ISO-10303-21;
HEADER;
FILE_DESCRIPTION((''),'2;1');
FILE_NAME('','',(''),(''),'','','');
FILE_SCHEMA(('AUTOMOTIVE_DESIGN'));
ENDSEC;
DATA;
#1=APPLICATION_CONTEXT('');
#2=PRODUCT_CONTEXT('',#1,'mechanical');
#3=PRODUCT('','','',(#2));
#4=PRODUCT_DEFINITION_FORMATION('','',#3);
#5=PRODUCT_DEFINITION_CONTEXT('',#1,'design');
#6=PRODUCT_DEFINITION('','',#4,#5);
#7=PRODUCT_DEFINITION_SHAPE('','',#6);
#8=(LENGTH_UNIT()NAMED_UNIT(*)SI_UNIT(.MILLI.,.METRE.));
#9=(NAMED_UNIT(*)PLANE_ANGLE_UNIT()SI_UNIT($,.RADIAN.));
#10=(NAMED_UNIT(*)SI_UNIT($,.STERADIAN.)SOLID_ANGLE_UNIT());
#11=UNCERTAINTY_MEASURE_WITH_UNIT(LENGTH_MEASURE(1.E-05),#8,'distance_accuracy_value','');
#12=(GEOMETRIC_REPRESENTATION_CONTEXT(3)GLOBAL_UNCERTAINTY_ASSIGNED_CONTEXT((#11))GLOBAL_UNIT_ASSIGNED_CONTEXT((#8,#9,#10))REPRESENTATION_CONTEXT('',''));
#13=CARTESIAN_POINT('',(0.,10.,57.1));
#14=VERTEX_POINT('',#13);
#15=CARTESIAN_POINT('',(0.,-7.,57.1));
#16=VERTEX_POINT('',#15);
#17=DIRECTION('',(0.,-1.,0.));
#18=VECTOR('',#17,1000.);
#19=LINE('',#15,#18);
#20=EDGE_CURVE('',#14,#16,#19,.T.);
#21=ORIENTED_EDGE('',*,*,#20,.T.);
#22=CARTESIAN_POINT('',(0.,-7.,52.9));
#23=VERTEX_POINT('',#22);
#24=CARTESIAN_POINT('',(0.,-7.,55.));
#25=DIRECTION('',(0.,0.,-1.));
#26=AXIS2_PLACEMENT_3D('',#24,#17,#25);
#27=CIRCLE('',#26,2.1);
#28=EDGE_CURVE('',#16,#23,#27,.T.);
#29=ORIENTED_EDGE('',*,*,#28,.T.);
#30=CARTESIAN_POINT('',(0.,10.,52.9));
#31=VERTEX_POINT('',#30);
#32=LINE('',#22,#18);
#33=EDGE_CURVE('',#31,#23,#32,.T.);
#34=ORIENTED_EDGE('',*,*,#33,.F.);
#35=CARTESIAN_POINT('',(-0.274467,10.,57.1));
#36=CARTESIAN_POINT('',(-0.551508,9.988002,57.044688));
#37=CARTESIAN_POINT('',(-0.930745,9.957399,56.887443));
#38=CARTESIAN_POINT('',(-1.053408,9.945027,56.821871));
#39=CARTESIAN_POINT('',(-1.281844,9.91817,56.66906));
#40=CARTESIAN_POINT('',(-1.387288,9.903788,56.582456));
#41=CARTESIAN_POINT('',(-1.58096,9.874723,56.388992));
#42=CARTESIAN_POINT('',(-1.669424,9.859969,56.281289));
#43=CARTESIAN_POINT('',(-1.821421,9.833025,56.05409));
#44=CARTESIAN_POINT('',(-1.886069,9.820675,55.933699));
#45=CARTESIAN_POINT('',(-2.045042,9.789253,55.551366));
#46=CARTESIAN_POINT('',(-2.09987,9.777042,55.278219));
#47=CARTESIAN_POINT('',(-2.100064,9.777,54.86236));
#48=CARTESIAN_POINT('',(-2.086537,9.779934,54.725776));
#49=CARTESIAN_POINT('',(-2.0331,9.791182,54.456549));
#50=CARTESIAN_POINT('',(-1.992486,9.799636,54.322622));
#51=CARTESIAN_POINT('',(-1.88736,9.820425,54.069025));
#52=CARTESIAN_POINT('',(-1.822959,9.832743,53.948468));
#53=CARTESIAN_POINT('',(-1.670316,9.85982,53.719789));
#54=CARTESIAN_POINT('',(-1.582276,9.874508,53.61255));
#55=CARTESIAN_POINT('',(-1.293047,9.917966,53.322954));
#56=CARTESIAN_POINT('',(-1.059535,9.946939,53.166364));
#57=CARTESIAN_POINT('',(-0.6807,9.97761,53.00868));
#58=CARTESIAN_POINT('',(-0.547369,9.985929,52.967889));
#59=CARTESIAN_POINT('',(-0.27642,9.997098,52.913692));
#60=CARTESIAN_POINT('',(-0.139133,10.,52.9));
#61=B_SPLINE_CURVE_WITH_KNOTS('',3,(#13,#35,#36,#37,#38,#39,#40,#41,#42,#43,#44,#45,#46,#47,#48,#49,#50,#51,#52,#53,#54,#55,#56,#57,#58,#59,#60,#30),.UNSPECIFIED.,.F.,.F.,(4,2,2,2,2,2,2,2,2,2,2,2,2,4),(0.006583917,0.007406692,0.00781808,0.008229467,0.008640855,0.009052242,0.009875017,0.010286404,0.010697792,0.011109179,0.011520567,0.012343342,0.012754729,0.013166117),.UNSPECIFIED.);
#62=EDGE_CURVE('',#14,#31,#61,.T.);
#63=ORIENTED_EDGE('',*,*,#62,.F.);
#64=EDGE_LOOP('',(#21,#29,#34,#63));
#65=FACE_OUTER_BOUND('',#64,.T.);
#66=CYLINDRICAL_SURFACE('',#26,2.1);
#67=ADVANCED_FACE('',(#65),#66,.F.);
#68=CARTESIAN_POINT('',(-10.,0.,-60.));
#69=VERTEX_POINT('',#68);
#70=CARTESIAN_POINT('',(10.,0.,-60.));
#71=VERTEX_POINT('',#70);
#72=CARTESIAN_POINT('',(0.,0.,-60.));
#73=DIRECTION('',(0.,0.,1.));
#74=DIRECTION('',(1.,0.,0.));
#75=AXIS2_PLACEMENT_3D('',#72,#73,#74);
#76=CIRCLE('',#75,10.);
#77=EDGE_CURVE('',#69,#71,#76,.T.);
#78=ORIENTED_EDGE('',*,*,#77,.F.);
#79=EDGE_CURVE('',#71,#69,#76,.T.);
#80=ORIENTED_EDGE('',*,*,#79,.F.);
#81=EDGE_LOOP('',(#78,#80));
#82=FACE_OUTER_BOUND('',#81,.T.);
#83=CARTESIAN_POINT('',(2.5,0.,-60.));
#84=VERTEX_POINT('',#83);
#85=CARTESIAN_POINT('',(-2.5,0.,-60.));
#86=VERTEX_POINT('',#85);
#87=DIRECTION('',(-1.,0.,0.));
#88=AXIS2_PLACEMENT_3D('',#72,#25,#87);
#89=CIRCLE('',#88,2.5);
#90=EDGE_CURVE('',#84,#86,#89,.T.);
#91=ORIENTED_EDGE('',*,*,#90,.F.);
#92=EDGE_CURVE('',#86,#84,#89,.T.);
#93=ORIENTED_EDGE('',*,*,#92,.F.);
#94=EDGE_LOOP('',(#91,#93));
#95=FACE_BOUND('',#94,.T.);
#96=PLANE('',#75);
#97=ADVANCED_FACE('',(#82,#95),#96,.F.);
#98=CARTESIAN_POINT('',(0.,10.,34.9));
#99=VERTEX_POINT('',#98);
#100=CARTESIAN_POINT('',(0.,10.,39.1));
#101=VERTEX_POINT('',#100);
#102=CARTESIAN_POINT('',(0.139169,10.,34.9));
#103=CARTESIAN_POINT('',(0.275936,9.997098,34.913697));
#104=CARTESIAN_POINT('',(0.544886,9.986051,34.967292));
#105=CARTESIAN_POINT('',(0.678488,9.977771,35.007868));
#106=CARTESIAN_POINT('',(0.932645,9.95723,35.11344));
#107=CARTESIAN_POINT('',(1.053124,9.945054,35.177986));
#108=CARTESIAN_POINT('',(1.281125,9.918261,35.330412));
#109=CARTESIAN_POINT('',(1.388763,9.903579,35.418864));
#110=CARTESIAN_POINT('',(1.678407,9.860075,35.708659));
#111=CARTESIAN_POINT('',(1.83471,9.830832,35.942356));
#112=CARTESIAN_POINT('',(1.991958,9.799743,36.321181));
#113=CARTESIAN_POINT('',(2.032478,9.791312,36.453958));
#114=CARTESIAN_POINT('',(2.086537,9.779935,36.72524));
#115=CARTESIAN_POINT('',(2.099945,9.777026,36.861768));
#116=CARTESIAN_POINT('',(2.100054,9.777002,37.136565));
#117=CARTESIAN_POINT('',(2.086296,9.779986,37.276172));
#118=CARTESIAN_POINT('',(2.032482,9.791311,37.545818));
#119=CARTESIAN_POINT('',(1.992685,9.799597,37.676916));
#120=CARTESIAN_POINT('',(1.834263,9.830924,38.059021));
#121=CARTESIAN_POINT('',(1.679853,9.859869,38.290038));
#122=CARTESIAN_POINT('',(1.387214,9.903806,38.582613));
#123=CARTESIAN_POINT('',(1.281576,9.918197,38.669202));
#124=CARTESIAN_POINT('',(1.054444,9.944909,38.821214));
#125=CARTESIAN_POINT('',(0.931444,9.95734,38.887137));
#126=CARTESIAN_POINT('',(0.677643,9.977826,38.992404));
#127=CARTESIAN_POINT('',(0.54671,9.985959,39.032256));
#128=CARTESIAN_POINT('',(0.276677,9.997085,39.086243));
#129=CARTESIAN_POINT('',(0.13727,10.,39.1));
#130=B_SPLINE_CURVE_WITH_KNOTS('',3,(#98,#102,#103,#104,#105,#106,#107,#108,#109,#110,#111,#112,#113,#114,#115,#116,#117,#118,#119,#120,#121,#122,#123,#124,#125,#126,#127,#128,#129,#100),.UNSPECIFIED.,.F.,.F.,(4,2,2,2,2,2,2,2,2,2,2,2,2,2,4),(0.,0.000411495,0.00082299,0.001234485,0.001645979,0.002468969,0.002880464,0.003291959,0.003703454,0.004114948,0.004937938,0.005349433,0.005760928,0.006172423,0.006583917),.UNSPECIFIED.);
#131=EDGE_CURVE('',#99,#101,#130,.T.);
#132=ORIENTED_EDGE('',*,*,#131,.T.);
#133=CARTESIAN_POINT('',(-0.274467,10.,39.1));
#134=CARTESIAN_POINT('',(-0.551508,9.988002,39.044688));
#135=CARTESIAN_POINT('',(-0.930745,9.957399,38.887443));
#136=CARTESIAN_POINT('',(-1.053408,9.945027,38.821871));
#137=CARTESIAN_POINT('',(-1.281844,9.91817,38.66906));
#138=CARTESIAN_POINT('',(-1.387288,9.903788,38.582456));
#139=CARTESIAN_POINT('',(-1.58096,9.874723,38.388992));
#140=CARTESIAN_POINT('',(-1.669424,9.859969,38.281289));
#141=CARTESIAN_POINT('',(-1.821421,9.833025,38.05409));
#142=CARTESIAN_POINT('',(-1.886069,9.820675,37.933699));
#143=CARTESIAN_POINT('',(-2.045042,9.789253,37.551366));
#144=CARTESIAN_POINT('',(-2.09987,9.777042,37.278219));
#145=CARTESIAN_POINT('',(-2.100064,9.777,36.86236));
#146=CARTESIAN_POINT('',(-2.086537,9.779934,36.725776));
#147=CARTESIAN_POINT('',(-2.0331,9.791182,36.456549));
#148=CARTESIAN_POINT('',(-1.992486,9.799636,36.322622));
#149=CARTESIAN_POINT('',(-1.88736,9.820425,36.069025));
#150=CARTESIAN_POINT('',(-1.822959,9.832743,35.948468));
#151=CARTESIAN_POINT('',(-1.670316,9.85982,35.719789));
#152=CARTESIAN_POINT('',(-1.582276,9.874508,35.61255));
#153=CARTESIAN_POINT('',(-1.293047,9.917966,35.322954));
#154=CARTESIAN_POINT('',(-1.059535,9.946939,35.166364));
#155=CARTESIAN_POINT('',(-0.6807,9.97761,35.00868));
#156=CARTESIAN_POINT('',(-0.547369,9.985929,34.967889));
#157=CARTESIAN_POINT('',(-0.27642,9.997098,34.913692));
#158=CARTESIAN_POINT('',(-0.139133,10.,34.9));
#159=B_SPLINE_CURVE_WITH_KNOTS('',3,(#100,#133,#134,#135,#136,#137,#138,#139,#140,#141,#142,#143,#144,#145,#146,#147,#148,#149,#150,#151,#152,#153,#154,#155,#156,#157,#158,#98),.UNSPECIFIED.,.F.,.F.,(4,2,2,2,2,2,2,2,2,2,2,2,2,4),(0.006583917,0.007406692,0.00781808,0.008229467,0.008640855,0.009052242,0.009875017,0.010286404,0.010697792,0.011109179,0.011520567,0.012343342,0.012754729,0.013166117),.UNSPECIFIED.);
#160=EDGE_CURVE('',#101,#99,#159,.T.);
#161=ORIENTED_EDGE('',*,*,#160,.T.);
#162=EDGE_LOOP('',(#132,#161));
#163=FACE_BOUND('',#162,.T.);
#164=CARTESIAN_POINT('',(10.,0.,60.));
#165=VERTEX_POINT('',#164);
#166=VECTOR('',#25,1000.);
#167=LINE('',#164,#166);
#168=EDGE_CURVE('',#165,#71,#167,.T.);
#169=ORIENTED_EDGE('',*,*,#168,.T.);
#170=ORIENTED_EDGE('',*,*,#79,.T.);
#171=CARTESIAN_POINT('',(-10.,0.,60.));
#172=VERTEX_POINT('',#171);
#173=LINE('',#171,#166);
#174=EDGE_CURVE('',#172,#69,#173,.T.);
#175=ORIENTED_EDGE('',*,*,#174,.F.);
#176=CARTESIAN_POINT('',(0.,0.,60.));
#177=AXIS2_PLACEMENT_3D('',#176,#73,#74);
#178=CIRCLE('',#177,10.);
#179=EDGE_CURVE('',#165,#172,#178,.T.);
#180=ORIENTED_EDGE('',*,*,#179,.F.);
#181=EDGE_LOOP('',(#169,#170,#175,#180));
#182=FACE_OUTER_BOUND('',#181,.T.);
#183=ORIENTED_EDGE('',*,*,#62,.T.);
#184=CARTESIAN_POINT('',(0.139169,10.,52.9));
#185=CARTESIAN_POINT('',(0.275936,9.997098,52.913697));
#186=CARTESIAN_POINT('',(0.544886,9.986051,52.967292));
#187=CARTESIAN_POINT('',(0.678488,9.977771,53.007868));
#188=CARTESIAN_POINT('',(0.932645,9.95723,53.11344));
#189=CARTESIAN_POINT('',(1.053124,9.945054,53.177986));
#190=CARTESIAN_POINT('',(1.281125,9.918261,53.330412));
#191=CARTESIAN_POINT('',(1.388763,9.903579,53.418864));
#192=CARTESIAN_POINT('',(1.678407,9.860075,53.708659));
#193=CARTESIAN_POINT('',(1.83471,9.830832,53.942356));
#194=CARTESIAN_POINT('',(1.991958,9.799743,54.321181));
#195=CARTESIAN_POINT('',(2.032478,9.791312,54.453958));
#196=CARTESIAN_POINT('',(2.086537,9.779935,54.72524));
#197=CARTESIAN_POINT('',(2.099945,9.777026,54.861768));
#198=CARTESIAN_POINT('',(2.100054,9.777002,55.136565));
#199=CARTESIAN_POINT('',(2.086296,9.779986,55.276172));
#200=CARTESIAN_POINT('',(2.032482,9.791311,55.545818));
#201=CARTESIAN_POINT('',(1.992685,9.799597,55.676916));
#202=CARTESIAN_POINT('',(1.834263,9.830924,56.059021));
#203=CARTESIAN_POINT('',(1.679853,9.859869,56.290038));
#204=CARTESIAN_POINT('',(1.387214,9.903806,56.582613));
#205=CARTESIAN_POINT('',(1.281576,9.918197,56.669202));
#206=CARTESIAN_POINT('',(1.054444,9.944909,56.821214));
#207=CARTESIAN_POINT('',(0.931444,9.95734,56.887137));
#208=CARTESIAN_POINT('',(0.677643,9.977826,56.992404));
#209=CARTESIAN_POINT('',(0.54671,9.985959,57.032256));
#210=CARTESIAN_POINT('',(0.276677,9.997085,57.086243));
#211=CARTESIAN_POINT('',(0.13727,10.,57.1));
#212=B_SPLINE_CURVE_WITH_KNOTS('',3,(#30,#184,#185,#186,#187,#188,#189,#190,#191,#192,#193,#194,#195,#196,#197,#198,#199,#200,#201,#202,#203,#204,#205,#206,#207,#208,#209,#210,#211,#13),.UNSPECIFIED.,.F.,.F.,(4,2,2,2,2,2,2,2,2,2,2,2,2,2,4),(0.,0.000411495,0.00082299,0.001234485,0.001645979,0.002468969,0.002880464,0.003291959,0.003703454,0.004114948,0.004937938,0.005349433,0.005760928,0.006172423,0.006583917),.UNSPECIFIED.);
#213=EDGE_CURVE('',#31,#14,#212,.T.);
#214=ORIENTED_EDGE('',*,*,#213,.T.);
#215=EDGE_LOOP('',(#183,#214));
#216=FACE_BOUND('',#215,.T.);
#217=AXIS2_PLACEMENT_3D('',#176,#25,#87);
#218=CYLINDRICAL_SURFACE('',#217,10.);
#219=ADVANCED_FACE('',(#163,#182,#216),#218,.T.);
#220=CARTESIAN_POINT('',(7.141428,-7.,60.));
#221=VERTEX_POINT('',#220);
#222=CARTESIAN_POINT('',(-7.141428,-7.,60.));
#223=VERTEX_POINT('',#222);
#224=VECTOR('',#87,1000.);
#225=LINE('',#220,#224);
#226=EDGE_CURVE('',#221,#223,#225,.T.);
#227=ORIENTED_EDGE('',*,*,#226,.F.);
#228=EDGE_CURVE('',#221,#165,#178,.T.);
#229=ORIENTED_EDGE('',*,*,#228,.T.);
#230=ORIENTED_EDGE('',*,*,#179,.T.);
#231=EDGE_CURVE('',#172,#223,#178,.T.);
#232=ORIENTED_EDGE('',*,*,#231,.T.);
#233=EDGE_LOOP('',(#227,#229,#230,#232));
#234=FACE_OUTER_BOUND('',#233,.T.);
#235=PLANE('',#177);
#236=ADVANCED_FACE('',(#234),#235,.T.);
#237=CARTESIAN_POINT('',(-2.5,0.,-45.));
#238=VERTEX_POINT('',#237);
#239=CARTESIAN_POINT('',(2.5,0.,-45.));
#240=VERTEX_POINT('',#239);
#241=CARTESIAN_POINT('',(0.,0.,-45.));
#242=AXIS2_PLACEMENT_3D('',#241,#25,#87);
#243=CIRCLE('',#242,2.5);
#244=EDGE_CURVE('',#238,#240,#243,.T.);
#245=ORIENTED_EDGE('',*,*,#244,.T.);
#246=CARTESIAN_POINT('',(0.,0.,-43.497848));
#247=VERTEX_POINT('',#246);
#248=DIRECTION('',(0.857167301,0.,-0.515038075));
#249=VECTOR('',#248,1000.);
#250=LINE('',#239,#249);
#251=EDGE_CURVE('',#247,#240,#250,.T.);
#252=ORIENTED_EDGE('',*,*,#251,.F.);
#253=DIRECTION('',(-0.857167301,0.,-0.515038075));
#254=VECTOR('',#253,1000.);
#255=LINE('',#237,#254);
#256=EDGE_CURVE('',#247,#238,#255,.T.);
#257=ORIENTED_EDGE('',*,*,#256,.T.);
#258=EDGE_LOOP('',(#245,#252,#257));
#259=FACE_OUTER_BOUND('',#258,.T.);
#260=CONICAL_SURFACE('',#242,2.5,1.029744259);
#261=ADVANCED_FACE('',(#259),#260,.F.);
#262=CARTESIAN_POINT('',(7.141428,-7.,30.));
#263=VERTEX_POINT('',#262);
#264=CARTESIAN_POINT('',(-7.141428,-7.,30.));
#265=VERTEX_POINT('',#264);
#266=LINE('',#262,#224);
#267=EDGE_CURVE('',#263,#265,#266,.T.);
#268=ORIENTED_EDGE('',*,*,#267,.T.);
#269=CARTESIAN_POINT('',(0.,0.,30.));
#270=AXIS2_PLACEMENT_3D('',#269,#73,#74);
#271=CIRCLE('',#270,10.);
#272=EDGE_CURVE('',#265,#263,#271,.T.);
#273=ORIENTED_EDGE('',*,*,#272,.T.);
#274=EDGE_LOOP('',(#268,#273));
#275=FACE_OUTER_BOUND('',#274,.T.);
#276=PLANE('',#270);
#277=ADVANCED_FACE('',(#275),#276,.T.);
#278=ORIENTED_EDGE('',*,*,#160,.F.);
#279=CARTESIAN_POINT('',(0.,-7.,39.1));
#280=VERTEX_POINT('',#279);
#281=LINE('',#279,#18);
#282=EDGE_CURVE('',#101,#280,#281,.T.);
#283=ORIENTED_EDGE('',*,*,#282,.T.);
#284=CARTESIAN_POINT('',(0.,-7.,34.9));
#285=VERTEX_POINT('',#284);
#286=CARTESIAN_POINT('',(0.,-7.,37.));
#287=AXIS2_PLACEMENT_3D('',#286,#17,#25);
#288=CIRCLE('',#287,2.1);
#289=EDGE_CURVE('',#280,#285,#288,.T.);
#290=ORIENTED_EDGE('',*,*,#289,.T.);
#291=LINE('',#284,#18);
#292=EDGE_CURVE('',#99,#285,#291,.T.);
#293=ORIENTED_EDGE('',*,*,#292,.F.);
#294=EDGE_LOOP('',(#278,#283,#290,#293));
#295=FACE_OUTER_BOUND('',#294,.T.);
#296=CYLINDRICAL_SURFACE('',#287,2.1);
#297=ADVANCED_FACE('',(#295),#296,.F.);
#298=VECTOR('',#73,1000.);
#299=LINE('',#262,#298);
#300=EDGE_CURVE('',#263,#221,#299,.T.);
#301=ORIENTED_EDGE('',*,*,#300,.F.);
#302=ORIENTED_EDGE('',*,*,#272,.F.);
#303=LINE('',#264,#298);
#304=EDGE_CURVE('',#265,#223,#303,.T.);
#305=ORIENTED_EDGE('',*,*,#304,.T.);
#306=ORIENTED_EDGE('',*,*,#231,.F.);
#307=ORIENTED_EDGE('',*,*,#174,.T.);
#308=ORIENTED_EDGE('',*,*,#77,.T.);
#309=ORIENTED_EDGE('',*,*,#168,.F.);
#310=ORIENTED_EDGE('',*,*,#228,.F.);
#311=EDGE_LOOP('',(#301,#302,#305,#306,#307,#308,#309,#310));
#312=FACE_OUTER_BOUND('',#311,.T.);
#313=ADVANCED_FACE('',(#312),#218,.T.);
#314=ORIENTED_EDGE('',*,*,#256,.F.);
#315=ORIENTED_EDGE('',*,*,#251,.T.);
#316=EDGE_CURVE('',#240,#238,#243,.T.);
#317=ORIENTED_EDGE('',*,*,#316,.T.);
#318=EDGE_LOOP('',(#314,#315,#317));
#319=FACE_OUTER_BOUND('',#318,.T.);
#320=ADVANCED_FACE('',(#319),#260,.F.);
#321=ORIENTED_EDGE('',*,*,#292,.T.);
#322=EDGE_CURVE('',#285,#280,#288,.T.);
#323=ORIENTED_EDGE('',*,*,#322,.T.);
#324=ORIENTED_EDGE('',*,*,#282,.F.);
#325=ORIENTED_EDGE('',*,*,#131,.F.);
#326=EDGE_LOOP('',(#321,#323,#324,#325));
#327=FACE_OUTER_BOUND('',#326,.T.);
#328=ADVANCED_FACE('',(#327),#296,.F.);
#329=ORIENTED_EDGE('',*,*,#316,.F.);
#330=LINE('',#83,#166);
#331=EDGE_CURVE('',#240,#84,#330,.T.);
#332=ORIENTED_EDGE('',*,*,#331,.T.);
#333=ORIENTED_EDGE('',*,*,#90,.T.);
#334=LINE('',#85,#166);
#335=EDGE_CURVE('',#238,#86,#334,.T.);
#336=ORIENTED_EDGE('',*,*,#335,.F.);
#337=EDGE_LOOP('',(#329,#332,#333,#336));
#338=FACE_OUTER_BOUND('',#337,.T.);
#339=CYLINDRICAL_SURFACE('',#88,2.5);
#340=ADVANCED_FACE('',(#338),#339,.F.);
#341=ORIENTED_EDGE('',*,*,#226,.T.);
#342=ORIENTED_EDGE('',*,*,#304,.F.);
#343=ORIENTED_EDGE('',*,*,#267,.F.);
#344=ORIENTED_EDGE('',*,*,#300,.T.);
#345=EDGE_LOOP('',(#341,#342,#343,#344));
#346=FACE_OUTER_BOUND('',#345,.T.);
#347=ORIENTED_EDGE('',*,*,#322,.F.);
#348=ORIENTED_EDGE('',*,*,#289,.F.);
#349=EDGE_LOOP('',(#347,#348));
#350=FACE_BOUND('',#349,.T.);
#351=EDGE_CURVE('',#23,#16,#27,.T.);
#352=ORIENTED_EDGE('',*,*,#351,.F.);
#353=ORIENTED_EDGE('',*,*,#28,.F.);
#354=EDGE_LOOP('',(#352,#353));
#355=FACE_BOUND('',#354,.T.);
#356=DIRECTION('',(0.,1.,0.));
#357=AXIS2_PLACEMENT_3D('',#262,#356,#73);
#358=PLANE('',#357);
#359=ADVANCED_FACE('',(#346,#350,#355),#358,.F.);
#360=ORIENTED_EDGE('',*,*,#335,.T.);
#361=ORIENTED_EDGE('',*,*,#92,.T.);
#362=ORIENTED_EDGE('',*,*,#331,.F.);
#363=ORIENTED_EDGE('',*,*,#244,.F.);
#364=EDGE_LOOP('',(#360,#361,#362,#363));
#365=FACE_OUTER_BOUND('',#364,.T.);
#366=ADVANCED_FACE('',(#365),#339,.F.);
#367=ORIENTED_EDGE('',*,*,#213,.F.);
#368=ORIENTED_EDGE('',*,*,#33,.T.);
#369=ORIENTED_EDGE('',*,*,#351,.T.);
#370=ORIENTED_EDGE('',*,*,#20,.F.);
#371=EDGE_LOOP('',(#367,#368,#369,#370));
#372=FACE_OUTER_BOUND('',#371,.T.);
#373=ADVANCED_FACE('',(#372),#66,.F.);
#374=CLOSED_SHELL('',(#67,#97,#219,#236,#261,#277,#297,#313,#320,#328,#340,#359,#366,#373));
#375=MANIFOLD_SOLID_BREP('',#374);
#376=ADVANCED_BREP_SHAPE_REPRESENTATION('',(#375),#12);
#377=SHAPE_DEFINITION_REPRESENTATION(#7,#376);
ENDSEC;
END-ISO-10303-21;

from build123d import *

# Parameters (mm, degrees)
SKETCH_1_R             = 10
EXTRUDE_1_DEPTH        = 60
HOLE_WIZARD_M6_1_D     = 5
HOLE_WIZARD_M6_1_DEPTH = 15
HOLE_WIZARD_M6_1_TIP   = 1.502151548
SKETCH_5_W             = 14.282856858
SKETCH_5_H             = 6
CUT_EXTRUDE_1_DEPTH    = 30
HOLE_WIZARD_M5_1_D     = 4.2


with BuildPart() as part:
    # 草图1 → 凸台-拉伸1 (new, symmetric)
    with BuildSketch(Plane.XY):
        Circle(SKETCH_1_R)
    extrude(amount=EXTRUDE_1_DEPTH, both=True)

    # M6 螺纹孔1
    with Locations(Plane(origin=(0, 0, -60), x_dir=(-1, 0, 0), z_dir=(0, 0, -1))):
        with Locations((0, 0)):
            Hole(HOLE_WIZARD_M6_1_D / 2, depth=HOLE_WIZARD_M6_1_DEPTH)
            with Locations((0, 0, -(HOLE_WIZARD_M6_1_DEPTH + HOLE_WIZARD_M6_1_TIP / 2))):  # 118° drill point
                Cone(0, HOLE_WIZARD_M6_1_D / 2, HOLE_WIZARD_M6_1_TIP, mode=Mode.SUBTRACT)

    # 草图5 → 切除-拉伸1 (cut)
    with BuildSketch(Plane.XY.offset(60)):
        with Locations((0, -10)):
            Rectangle(SKETCH_5_W, SKETCH_5_H)
    extrude(amount=-CUT_EXTRUDE_1_DEPTH, mode=Mode.SUBTRACT)

    # M5 螺纹孔1 (through all)
    with Locations(Plane(origin=(0, -7, 0), x_dir=(-1, 0, 0), z_dir=(0, -1, 0))):
        with Locations((0, -55), (0, -37)):
            Hole(HOLE_WIZARD_M5_1_D / 2)


solid = part.part
